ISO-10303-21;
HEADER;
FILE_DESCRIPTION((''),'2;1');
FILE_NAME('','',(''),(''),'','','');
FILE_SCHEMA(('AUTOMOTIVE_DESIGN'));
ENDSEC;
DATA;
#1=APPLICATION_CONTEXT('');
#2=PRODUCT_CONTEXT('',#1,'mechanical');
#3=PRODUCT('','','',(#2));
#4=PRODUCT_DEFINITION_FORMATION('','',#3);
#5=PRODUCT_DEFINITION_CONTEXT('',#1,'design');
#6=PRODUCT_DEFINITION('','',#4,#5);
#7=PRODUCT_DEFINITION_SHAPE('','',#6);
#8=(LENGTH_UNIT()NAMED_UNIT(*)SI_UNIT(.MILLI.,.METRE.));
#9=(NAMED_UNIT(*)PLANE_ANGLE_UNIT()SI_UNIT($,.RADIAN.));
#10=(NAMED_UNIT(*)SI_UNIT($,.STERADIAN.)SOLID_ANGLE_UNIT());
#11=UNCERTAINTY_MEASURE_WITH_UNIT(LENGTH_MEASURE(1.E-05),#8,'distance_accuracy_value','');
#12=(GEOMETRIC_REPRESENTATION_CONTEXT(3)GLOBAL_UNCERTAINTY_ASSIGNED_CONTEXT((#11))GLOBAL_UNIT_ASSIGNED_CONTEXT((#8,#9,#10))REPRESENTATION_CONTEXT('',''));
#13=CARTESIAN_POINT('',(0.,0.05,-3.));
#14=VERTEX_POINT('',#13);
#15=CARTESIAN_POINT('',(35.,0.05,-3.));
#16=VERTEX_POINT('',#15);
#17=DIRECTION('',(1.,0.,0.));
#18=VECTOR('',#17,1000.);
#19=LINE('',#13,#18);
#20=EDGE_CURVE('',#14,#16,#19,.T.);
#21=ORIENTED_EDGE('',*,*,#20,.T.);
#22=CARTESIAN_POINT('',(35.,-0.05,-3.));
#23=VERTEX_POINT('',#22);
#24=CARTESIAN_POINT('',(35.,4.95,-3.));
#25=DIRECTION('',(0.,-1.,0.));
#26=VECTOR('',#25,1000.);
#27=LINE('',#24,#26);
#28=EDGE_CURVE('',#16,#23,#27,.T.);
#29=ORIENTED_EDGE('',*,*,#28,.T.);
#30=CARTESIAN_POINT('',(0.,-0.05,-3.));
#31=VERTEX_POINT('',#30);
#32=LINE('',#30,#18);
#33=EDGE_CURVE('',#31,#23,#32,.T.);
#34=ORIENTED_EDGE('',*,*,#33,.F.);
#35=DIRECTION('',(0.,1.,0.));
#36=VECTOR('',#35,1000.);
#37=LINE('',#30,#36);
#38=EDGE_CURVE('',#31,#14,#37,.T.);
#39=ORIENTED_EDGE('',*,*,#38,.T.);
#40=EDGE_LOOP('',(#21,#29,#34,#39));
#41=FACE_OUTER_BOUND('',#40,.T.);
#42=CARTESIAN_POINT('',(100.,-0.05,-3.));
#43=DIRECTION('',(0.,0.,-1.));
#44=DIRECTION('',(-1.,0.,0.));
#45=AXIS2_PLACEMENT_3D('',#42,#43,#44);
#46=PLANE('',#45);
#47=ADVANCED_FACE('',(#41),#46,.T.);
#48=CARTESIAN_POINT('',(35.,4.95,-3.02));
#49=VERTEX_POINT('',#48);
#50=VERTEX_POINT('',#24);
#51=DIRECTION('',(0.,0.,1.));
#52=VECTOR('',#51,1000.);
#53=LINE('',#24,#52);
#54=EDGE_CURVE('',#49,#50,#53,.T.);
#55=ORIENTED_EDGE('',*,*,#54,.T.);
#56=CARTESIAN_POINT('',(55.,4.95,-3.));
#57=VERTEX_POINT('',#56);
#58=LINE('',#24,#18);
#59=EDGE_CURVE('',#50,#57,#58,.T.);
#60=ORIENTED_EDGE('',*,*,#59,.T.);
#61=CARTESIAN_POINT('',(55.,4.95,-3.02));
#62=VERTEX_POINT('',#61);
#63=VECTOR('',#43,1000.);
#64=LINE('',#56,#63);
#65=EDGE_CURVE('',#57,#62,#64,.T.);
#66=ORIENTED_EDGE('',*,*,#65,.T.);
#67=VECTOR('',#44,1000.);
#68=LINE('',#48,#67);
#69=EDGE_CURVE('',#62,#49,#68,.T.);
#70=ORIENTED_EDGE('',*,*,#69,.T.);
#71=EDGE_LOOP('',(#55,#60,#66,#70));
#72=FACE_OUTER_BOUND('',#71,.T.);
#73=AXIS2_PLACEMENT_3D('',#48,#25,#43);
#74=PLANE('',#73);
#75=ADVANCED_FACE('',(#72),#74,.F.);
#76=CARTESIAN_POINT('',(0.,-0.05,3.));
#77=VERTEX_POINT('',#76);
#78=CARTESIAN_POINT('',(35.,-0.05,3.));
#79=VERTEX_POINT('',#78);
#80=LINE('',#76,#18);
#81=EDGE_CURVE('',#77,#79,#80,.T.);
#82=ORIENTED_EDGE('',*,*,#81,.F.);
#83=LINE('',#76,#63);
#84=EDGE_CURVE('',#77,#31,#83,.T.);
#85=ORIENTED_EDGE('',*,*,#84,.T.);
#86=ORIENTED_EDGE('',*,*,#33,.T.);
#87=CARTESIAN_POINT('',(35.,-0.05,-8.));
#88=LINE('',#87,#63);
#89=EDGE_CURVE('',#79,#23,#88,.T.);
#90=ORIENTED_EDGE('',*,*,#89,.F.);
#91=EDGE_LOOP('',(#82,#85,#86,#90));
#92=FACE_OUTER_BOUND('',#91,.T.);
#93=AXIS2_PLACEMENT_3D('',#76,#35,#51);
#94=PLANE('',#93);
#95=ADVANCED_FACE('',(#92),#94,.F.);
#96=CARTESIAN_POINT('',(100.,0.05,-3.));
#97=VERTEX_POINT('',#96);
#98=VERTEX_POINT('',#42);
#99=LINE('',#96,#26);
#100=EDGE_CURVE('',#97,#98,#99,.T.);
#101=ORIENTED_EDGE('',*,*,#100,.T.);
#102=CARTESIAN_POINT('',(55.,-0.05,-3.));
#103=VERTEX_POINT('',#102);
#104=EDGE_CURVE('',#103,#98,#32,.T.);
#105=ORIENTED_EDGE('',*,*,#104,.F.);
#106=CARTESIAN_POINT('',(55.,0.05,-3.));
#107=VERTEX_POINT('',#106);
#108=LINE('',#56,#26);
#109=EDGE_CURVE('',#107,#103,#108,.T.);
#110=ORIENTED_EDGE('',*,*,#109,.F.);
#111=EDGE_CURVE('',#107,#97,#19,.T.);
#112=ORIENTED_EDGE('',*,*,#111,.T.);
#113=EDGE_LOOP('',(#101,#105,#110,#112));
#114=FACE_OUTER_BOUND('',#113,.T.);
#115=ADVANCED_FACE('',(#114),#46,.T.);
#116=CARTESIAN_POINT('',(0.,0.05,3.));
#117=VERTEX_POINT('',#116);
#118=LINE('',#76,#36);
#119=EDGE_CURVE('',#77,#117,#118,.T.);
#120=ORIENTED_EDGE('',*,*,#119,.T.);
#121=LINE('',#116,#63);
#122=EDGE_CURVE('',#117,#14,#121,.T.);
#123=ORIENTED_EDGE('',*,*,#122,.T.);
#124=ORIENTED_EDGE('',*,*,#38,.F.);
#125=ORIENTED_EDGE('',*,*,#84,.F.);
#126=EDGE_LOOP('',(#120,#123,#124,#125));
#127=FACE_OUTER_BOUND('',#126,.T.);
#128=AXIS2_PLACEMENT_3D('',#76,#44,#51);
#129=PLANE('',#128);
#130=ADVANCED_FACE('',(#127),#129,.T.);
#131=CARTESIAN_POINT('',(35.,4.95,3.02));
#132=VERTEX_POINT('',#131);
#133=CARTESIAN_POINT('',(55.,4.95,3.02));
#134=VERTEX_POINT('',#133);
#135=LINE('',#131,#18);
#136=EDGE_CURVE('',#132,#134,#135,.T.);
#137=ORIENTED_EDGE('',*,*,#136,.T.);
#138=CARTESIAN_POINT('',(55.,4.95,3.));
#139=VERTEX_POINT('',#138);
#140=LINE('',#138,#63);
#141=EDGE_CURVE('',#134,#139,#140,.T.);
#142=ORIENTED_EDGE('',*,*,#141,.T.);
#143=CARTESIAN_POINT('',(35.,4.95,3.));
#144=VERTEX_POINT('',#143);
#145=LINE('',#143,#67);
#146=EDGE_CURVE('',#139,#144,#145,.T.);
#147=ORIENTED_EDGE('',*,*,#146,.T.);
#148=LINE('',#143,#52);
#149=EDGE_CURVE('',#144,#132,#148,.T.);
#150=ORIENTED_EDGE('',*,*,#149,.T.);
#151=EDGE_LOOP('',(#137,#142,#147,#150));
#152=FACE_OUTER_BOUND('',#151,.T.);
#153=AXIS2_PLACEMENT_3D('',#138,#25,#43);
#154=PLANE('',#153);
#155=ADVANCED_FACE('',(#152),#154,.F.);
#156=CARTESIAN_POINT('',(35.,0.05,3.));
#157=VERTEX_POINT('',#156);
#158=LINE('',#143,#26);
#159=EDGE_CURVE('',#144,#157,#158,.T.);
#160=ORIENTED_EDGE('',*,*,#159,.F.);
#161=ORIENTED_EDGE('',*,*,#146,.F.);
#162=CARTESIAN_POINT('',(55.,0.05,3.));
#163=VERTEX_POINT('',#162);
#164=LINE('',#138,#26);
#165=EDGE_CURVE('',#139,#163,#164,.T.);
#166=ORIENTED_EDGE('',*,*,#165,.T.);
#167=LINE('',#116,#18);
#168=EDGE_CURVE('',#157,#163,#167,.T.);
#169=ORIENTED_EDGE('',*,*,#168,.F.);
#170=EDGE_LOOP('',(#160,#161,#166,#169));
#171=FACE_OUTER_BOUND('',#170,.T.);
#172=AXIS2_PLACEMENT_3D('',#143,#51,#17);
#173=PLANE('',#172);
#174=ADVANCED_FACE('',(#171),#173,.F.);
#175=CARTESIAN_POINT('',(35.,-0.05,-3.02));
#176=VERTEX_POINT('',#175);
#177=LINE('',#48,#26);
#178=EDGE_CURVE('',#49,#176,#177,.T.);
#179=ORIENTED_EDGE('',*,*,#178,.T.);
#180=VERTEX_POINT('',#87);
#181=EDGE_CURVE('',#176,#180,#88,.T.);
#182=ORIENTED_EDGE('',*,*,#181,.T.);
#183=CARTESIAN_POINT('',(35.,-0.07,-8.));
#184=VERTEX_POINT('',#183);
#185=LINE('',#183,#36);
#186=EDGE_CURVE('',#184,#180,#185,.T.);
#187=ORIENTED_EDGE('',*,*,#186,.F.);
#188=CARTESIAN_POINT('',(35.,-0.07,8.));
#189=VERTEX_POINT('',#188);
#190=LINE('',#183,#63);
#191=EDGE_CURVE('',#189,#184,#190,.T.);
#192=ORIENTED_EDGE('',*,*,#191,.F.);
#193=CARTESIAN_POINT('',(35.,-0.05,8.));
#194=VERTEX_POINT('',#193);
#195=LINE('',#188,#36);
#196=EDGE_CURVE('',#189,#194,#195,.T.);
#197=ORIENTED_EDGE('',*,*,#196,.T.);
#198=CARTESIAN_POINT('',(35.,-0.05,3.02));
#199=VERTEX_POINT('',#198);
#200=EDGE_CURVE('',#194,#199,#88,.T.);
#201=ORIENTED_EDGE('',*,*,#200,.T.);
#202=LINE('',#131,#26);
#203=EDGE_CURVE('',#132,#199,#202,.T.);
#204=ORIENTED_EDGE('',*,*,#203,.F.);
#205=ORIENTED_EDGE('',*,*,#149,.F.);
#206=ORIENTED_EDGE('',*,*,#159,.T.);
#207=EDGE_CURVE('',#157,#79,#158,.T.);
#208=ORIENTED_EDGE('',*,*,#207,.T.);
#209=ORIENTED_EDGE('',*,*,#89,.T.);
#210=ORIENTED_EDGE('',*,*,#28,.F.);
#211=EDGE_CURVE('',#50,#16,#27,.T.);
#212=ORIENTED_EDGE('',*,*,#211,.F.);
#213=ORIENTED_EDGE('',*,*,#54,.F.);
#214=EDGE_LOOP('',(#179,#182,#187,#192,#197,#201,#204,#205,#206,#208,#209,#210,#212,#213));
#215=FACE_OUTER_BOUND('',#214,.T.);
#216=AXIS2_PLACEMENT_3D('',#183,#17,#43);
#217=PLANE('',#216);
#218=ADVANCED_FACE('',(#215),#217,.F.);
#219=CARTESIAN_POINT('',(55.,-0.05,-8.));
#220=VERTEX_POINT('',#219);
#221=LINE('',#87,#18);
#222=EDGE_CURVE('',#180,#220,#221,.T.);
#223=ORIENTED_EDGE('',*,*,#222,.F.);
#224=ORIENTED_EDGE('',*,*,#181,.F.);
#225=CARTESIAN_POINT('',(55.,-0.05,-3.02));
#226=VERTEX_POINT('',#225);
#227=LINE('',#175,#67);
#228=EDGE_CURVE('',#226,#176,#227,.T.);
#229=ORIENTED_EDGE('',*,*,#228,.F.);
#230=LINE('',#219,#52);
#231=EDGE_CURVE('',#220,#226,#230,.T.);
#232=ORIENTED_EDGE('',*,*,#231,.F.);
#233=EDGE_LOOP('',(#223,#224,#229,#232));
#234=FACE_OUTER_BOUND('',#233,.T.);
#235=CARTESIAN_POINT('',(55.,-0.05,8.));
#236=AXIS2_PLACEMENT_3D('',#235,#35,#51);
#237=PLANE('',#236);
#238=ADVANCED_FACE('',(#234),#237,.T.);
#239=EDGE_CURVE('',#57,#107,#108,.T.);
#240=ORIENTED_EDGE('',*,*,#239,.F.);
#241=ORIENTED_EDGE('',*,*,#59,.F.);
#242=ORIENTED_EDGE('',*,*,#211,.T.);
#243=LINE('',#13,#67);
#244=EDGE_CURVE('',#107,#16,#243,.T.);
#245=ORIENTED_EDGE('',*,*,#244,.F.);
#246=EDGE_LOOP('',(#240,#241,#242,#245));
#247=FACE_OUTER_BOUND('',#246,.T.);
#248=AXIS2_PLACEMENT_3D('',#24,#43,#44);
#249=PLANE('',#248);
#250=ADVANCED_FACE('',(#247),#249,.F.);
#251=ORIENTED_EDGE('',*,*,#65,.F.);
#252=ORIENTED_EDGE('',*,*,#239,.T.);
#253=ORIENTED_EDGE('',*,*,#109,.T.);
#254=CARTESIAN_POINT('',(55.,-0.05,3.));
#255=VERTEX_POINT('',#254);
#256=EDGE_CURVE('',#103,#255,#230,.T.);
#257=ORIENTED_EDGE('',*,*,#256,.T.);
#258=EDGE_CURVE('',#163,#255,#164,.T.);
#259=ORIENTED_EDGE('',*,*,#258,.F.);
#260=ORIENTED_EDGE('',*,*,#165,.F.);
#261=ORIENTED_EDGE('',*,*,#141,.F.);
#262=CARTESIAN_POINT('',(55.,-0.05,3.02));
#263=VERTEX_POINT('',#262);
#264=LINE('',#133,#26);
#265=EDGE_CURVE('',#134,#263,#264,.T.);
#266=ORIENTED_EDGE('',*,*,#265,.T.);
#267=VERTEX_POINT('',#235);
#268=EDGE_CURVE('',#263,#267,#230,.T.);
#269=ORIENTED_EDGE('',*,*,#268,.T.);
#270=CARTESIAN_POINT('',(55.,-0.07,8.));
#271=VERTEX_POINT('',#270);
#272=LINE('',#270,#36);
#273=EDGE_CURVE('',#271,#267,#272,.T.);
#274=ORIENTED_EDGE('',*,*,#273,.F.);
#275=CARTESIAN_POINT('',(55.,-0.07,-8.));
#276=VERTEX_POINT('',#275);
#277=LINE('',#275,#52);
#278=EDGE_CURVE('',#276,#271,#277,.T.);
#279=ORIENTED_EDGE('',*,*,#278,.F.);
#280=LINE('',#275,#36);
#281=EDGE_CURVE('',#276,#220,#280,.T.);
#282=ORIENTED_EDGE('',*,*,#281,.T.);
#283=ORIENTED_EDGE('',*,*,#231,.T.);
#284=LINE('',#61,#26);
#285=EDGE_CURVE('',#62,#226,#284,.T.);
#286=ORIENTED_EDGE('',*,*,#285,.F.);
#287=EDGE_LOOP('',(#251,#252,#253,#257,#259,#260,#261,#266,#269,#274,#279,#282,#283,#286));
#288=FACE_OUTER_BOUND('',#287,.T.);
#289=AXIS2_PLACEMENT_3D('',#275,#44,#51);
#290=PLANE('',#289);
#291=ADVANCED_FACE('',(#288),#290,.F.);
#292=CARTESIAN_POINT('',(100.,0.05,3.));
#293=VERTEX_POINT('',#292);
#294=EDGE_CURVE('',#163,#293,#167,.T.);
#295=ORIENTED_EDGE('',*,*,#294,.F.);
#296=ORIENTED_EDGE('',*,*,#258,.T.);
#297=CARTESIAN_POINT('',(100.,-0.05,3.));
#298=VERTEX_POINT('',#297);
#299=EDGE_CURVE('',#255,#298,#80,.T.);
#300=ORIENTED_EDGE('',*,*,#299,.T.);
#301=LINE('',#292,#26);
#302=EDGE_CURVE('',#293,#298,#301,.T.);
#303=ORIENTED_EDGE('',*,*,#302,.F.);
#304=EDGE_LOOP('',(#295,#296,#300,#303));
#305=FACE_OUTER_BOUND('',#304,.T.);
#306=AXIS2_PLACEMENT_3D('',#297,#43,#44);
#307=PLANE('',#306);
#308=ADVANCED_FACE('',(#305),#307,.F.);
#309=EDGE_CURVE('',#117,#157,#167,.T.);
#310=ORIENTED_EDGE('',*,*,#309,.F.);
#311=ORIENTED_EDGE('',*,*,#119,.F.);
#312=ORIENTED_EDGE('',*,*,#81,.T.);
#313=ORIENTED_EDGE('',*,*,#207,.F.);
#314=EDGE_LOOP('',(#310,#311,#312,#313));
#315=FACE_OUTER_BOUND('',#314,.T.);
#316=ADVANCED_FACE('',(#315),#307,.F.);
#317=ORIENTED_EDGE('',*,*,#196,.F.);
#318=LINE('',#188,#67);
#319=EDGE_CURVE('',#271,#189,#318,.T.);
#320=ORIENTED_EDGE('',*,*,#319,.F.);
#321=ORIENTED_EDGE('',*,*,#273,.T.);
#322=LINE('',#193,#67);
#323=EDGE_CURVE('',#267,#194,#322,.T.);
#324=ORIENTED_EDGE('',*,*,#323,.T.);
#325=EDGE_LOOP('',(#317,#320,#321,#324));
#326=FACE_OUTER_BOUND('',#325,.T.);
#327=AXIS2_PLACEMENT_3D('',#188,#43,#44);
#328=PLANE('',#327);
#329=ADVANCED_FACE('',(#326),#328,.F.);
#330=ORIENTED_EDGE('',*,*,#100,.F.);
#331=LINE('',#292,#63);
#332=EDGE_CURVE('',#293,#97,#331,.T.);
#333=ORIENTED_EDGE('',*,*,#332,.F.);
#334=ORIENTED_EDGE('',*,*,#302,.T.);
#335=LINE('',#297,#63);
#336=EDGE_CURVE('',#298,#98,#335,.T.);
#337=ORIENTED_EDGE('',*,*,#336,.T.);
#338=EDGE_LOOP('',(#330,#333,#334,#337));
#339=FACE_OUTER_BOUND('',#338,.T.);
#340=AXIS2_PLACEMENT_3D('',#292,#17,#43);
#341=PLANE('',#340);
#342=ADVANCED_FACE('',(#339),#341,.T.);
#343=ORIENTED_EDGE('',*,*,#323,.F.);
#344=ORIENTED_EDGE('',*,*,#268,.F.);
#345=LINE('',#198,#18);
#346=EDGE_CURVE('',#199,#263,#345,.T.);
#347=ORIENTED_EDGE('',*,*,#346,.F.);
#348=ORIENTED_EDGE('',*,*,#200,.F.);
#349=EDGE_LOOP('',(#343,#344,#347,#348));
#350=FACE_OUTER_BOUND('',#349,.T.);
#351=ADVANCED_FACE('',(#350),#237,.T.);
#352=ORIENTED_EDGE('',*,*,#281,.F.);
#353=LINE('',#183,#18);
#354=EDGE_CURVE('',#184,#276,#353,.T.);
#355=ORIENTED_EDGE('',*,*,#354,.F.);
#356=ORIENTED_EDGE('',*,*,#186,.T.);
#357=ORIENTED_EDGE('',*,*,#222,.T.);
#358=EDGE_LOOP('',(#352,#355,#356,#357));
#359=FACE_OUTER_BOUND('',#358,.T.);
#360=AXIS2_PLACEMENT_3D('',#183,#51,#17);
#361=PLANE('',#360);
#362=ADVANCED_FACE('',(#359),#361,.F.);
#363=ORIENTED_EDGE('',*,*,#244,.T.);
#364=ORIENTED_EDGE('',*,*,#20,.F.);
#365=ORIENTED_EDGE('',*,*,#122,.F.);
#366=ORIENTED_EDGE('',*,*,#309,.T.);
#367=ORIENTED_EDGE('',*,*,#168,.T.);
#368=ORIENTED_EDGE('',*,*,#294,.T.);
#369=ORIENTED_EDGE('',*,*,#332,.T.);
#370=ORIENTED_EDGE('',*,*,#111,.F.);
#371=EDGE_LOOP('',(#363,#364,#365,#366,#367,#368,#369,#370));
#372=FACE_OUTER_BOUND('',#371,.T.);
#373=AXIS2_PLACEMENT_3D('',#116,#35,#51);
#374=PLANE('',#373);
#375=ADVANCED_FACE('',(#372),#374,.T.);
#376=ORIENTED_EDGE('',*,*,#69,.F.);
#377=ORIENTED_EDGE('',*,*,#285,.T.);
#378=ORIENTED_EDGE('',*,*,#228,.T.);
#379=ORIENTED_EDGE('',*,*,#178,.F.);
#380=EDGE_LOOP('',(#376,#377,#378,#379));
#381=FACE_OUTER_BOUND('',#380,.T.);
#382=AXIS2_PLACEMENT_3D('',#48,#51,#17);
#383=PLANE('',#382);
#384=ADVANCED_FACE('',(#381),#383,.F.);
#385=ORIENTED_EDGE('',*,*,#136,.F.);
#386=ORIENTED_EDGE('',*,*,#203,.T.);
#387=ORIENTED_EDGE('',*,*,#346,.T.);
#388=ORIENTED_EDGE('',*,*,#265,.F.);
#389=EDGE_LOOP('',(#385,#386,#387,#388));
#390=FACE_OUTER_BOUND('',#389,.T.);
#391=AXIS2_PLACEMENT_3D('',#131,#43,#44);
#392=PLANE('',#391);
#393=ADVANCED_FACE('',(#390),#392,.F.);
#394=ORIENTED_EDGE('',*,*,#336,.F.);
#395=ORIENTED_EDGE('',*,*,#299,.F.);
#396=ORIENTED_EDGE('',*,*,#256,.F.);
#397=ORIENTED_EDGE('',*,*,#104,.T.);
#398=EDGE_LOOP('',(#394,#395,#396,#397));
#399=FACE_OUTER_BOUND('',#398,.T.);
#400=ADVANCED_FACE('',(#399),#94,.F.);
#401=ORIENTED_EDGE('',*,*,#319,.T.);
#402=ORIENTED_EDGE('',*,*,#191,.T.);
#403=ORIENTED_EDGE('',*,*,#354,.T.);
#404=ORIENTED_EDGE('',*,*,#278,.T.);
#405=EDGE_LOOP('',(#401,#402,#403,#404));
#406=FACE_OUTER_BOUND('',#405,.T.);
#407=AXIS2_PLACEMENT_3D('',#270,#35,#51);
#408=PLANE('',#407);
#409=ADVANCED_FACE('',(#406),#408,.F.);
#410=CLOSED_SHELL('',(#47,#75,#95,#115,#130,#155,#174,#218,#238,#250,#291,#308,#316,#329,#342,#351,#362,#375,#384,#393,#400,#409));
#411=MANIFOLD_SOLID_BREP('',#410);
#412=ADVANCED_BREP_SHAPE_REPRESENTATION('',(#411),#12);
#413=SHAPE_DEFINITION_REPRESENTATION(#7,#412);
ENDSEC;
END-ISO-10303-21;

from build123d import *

# Parameters (mm, degrees)
SKETCH1_W           = 100
SKETCH1_H           = 0.1
EXTRUDE_THIN1_DEPTH = 3
SKETCH2_W           = 20
SKETCH2_H           = 16
BOSS_EXTRUDE1_DEPTH = 0.02
SKETCH3_W           = 20
SKETCH3_H           = 0.02
BOSS_EXTRUDE2_DEPTH = 5


with BuildPart() as part:
    # Sketch1 → Extrude-Thin1 (new, symmetric)
    with BuildSketch(Plane.XY):
        with Locations((50, 0)):
            Rectangle(SKETCH1_W, SKETCH1_H)
    extrude(amount=EXTRUDE_THIN1_DEPTH, both=True)

    # Sketch2 → Boss-Extrude1 (add)
    with BuildSketch(Plane.XZ.offset(0.05)):
        with Locations((45, 0)):
            Rectangle(SKETCH2_W, SKETCH2_H)
    extrude(amount=BOSS_EXTRUDE1_DEPTH)

    # Sketch3 → Boss-Extrude2 (add)
    with BuildSketch(Plane(origin=(0, -0.05, 0), x_dir=(1, 0, 0), z_dir=(0, 1, 0))):
        with Locations((45, 3.01)):
            Rectangle(SKETCH3_W, SKETCH3_H)
        with Locations((45, -3.01)):
            Rectangle(SKETCH3_W, SKETCH3_H)
    extrude(amount=BOSS_EXTRUDE2_DEPTH)


solid = part.part
